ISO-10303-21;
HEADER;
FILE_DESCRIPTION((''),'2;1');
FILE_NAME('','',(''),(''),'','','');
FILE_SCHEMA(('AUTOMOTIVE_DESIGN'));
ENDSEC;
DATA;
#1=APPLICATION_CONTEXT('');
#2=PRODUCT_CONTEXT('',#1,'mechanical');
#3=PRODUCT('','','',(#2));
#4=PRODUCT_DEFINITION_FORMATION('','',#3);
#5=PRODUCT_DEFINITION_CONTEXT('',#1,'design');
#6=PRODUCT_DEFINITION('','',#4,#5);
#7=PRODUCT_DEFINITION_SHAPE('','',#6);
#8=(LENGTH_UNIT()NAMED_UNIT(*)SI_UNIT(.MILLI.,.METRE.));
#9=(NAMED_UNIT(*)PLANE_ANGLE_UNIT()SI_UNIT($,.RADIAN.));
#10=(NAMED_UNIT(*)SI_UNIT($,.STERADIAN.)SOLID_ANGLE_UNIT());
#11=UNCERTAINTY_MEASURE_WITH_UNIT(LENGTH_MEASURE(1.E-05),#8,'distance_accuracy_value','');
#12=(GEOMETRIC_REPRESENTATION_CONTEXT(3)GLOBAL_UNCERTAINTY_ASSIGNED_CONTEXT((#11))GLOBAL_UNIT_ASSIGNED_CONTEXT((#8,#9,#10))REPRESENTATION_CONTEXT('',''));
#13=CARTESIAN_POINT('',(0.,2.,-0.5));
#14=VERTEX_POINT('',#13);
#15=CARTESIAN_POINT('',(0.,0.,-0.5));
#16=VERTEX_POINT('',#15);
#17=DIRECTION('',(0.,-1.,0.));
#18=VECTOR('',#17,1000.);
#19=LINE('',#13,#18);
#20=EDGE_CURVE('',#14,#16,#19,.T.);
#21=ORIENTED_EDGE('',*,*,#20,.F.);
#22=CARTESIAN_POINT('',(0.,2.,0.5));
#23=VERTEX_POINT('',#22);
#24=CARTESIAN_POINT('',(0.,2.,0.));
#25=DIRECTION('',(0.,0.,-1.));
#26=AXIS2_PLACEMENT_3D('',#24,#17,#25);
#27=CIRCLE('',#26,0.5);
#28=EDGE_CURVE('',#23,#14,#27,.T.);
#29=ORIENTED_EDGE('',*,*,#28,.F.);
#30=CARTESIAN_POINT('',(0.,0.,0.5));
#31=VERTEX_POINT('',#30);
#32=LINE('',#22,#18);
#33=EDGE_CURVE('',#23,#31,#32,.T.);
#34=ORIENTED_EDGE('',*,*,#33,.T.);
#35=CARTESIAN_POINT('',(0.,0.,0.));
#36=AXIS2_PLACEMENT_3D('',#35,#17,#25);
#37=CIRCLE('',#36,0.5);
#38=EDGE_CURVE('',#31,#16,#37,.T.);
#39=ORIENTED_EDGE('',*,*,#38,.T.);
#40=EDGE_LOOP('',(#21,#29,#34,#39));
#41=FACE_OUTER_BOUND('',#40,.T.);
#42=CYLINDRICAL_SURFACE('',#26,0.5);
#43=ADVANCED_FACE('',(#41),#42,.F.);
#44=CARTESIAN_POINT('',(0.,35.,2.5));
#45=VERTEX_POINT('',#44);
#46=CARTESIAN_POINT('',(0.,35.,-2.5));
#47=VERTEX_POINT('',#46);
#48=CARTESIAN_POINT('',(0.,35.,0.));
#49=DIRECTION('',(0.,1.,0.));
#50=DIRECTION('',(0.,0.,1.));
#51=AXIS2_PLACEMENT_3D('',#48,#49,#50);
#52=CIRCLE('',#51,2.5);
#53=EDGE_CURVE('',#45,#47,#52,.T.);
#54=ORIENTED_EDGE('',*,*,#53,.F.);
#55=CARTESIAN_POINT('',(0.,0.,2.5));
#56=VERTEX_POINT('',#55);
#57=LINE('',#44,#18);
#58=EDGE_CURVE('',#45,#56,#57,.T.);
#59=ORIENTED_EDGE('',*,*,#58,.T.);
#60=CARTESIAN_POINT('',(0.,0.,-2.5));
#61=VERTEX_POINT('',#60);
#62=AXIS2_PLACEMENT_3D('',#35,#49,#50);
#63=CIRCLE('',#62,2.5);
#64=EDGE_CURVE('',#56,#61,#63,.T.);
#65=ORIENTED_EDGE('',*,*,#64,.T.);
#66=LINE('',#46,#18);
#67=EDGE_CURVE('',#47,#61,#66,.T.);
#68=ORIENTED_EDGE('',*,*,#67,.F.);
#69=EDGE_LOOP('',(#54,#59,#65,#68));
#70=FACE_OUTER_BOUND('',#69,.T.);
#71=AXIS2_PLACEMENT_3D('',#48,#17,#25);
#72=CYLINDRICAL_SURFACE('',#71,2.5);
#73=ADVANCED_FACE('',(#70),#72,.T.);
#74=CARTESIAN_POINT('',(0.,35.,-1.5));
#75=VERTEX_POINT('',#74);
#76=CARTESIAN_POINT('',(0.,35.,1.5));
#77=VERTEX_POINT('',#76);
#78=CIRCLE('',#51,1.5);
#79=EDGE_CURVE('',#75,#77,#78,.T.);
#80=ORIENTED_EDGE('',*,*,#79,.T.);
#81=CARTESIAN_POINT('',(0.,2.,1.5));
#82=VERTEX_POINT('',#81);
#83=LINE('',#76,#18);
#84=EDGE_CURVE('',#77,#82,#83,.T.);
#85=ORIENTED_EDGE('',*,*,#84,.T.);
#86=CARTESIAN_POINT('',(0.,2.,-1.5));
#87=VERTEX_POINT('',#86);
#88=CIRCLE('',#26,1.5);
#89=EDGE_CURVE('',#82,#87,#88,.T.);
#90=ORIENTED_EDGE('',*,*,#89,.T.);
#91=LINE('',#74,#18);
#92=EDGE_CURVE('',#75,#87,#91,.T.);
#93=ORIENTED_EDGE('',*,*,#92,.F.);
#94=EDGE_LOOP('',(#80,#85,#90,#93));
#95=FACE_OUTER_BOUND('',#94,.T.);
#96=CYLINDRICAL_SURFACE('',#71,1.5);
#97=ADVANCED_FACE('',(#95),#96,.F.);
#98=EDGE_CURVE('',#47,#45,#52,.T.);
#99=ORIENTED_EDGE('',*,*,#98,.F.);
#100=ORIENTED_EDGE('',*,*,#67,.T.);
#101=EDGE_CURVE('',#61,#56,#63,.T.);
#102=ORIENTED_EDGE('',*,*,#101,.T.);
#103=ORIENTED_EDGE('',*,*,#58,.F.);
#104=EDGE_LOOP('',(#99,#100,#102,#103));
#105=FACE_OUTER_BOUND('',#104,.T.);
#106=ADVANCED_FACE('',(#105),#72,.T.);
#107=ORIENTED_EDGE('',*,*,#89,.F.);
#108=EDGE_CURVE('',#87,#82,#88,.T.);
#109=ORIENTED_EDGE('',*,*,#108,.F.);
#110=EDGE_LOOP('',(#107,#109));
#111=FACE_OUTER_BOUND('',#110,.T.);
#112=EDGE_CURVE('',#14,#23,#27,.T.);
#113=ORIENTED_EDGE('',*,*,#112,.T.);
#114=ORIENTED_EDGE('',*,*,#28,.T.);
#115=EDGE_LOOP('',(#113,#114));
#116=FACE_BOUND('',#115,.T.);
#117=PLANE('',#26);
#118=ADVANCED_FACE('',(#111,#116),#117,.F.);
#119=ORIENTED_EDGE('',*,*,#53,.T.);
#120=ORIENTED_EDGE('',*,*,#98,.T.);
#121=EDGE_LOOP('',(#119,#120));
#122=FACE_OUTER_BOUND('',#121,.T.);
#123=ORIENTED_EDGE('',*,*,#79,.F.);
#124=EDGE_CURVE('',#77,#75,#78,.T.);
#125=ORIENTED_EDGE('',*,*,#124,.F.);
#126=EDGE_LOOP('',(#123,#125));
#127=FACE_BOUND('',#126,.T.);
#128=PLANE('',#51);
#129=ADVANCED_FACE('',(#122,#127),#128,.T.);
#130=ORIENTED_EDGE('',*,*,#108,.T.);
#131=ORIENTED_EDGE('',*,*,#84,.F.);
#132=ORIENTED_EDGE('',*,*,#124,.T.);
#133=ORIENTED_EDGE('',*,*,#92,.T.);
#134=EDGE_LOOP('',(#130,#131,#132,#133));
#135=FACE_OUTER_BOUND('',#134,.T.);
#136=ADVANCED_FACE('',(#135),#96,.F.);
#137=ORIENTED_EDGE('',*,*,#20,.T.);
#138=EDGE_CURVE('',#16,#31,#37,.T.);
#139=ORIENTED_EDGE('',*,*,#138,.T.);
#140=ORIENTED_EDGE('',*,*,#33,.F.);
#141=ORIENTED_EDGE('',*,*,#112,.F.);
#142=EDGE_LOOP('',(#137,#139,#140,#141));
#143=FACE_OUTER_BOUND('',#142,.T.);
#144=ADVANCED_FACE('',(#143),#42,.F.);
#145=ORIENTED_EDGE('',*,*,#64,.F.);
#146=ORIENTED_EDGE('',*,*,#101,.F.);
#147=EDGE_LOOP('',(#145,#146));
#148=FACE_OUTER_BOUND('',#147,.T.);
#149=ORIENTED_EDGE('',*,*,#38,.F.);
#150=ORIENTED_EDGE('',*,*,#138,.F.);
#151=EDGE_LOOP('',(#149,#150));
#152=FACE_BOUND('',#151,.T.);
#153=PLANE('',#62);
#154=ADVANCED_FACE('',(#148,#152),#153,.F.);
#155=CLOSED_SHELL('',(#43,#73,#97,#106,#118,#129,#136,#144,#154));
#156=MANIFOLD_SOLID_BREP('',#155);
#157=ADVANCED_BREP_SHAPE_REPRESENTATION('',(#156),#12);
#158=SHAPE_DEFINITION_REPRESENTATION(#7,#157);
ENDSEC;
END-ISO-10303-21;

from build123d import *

# Parameters (mm, degrees)
SKETCH1_R           = 2.5
SKETCH1_R_2         = 1.5
BOSS_EXTRUDE1_DEPTH = 35
SKETCH2_R           = 1.5
SKETCH2_R_2         = 0.5
BOSS_EXTRUDE2_DEPTH = 2


with BuildPart() as part:
    # Sketch1 → Boss-Extrude1 (new body)
    with BuildSketch(Plane(origin=(0, 0, 0), x_dir=(1, 0, 0), z_dir=(0, 1, 0))):
        with Locations(Location((0, 0, 0), (0, 0, 270))):
            Circle(SKETCH1_R)
        with Locations(Location((0, 0, 0), (0, 0, 270))):
            Circle(SKETCH1_R_2, mode=Mode.SUBTRACT)
    extrude(amount=BOSS_EXTRUDE1_DEPTH)

    # Sketch2 → Boss-Extrude2 (add)
    with BuildSketch(Plane.XZ):
        with Locations(Location((0, 0, 0), (0, 0, 270))):
            Circle(SKETCH2_R)
        with Locations(Location((0, 0, 0), (0, 0, 270))):
            Circle(SKETCH2_R_2, mode=Mode.SUBTRACT)
    extrude(amount=-BOSS_EXTRUDE2_DEPTH)


solid = part.part
